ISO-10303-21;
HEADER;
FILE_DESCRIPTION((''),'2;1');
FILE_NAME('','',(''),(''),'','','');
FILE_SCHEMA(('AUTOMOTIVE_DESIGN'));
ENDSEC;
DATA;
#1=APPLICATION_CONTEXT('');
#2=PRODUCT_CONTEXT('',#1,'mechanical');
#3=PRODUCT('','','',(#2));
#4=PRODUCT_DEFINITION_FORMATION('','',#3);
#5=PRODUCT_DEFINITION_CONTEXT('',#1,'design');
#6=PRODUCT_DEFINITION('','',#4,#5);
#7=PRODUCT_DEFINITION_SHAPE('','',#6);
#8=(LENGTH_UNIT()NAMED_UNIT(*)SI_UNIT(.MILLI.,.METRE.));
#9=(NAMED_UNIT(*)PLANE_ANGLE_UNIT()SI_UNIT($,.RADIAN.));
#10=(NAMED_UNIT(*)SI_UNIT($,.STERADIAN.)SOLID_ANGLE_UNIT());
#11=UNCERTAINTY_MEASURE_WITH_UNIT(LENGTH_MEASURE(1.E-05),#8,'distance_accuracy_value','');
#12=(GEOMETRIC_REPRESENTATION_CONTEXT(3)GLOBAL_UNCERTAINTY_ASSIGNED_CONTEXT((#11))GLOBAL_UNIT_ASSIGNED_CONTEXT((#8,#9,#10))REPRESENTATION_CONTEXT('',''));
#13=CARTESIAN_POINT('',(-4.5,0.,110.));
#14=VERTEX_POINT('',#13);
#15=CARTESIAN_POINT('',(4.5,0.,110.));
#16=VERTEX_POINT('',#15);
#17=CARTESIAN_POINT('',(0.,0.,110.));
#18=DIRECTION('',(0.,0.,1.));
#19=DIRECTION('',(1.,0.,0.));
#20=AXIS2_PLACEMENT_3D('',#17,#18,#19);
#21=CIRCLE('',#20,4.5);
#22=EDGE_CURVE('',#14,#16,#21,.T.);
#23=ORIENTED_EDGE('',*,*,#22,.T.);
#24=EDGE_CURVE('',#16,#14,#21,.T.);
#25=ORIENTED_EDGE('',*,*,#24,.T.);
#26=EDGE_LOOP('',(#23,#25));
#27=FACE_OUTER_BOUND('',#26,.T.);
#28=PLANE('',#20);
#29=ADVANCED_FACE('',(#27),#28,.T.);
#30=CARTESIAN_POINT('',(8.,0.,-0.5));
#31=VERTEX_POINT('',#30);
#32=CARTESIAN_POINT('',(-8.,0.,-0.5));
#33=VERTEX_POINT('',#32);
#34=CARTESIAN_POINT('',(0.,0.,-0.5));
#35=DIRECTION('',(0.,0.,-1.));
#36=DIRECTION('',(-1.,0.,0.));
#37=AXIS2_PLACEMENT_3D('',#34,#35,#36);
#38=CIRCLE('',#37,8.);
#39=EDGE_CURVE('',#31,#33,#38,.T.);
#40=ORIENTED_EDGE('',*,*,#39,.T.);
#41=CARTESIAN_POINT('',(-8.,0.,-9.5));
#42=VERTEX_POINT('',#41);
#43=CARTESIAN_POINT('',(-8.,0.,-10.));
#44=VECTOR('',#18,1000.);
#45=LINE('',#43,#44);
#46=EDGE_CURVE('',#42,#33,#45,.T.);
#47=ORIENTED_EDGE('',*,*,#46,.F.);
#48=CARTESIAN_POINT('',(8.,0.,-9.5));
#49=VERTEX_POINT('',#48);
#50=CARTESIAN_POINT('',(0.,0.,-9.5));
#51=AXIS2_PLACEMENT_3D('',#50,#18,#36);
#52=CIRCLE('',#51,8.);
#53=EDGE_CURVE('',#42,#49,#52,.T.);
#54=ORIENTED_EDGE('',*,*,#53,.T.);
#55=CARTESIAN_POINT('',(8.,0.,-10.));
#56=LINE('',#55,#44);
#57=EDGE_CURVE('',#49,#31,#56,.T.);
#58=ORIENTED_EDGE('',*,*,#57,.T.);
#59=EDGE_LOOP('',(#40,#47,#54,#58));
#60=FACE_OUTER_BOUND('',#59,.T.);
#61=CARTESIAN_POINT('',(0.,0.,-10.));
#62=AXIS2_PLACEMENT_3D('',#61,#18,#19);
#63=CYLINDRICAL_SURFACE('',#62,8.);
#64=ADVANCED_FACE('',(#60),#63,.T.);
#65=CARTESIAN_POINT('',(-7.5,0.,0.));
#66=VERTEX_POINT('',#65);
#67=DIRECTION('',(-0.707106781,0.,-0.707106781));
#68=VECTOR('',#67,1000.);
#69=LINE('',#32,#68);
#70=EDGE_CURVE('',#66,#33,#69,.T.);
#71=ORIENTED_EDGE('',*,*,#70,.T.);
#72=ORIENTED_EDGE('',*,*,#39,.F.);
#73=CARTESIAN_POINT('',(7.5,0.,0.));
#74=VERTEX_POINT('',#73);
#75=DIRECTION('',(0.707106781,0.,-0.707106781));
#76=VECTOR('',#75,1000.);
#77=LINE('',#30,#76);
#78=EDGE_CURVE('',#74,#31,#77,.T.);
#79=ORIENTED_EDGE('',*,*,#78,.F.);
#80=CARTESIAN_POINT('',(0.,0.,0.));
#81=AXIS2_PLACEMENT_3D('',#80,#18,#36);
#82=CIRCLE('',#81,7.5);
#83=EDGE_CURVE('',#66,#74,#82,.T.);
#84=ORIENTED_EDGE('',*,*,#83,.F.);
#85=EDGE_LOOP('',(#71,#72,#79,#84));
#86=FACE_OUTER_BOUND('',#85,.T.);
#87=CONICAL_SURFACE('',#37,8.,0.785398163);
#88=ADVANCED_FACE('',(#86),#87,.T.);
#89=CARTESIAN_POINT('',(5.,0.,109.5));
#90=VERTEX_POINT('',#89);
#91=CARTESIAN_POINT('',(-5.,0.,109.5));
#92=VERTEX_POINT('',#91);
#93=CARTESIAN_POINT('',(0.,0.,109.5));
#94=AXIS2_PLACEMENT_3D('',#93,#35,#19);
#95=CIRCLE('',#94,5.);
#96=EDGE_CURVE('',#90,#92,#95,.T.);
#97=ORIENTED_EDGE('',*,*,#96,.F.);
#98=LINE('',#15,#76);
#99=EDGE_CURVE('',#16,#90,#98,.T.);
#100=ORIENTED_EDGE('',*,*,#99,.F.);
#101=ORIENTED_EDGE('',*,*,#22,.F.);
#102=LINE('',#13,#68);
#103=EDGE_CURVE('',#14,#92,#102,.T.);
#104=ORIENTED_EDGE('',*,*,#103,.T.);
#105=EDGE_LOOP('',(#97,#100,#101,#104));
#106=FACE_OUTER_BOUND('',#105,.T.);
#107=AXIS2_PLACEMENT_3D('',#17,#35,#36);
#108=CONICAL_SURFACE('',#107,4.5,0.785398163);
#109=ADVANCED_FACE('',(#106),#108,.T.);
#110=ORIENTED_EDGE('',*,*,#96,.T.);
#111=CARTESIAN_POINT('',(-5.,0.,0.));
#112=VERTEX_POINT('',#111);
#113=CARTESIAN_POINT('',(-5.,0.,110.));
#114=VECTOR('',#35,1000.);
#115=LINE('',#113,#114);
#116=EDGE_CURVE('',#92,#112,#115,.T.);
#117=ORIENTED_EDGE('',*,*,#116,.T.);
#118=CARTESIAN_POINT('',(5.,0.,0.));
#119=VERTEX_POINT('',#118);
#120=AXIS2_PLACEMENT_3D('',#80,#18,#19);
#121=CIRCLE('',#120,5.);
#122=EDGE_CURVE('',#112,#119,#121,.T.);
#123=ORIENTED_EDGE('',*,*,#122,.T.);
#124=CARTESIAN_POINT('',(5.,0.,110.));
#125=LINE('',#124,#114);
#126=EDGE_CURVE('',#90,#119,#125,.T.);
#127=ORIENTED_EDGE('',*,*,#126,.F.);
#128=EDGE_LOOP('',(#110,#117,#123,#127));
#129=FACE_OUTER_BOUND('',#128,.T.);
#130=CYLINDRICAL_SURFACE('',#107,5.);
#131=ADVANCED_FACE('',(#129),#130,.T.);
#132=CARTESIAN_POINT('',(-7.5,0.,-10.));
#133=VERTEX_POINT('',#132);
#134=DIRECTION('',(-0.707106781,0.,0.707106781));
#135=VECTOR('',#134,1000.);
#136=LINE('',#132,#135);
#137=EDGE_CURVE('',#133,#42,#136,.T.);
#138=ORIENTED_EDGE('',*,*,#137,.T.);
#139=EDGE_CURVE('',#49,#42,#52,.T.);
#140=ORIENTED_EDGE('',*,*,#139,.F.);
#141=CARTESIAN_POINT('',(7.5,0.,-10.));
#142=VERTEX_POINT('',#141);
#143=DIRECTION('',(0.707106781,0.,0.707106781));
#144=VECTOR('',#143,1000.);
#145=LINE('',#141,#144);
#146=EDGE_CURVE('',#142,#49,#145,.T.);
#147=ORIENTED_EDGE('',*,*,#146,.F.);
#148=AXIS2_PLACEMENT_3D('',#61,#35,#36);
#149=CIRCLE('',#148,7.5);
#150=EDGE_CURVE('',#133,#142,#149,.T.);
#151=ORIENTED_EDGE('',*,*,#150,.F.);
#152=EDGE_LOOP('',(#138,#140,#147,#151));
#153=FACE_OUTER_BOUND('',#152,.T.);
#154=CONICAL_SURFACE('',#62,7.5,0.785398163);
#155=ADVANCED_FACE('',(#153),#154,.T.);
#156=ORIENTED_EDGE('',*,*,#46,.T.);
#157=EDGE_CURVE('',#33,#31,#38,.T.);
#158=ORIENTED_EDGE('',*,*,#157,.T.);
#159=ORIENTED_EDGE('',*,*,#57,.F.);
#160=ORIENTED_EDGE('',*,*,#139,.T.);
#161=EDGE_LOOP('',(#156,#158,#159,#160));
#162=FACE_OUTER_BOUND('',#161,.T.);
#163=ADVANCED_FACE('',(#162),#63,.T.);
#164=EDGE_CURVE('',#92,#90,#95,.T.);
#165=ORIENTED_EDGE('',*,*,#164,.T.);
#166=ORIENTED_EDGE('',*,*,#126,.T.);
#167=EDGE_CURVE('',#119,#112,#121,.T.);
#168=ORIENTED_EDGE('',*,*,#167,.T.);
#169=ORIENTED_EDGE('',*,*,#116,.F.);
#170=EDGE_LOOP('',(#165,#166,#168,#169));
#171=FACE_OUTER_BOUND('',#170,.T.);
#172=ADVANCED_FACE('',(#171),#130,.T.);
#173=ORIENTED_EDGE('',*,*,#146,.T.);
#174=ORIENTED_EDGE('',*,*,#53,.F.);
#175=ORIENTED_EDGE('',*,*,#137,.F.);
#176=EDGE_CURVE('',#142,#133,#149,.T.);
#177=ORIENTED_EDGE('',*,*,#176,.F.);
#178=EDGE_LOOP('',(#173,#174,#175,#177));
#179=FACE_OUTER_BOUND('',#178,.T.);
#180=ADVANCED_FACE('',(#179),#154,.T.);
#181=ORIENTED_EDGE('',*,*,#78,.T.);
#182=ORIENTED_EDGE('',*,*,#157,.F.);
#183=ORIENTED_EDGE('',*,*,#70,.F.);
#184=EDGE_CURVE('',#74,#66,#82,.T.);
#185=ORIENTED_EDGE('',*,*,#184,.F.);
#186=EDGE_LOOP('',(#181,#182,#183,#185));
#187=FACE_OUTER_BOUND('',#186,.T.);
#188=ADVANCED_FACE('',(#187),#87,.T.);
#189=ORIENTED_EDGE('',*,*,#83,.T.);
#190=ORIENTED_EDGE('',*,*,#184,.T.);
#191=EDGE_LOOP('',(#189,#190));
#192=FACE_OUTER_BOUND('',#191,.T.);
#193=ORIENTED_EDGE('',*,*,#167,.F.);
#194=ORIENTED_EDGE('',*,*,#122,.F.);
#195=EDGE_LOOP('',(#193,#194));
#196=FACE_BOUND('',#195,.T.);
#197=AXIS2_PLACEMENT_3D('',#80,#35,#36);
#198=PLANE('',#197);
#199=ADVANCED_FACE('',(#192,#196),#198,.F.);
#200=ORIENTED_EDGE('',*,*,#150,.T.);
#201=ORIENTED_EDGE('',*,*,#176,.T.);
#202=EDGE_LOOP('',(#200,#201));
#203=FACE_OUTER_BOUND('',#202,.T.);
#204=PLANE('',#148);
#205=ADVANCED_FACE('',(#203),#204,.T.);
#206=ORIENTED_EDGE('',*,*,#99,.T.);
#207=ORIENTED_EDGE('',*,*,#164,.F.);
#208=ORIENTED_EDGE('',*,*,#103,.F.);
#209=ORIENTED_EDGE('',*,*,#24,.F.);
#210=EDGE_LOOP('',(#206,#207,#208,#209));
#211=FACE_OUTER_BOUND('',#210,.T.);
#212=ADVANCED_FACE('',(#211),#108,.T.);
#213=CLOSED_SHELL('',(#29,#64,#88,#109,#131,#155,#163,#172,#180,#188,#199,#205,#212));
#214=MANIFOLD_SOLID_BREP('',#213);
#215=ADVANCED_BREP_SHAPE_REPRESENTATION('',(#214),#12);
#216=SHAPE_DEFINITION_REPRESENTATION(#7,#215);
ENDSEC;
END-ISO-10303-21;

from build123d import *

# Parameters (mm, degrees)
SKETCH1_R           = 5
BOSS_EXTRUDE1_DEPTH = 110
SKETCH2_R           = 8
BOSS_EXTRUDE2_DEPTH = 10
CHAMFER1_SIZE       = 0.5


with BuildPart() as part:
    # Sketch1 → Boss-Extrude1 (new body)
    with BuildSketch(Plane.XY):
        Circle(SKETCH1_R)
    extrude(amount=BOSS_EXTRUDE1_DEPTH)

    # Sketch2 → Boss-Extrude2 (add)
    with BuildSketch(Plane(origin=(0, 0, 0), x_dir=(-1, 0, 0), z_dir=(0, 0, -1))):
        Circle(SKETCH2_R)
    extrude(amount=BOSS_EXTRUDE2_DEPTH)

    # Chamfer1
    chamfer1_edges = [part.edges().sort_by_distance(p)[0] for p in [
        (-5, 0, 110),
        (8, 0, 0),
        (8, 0, -10),
    ]]
    chamfer(chamfer1_edges, length=CHAMFER1_SIZE)


solid = part.part
